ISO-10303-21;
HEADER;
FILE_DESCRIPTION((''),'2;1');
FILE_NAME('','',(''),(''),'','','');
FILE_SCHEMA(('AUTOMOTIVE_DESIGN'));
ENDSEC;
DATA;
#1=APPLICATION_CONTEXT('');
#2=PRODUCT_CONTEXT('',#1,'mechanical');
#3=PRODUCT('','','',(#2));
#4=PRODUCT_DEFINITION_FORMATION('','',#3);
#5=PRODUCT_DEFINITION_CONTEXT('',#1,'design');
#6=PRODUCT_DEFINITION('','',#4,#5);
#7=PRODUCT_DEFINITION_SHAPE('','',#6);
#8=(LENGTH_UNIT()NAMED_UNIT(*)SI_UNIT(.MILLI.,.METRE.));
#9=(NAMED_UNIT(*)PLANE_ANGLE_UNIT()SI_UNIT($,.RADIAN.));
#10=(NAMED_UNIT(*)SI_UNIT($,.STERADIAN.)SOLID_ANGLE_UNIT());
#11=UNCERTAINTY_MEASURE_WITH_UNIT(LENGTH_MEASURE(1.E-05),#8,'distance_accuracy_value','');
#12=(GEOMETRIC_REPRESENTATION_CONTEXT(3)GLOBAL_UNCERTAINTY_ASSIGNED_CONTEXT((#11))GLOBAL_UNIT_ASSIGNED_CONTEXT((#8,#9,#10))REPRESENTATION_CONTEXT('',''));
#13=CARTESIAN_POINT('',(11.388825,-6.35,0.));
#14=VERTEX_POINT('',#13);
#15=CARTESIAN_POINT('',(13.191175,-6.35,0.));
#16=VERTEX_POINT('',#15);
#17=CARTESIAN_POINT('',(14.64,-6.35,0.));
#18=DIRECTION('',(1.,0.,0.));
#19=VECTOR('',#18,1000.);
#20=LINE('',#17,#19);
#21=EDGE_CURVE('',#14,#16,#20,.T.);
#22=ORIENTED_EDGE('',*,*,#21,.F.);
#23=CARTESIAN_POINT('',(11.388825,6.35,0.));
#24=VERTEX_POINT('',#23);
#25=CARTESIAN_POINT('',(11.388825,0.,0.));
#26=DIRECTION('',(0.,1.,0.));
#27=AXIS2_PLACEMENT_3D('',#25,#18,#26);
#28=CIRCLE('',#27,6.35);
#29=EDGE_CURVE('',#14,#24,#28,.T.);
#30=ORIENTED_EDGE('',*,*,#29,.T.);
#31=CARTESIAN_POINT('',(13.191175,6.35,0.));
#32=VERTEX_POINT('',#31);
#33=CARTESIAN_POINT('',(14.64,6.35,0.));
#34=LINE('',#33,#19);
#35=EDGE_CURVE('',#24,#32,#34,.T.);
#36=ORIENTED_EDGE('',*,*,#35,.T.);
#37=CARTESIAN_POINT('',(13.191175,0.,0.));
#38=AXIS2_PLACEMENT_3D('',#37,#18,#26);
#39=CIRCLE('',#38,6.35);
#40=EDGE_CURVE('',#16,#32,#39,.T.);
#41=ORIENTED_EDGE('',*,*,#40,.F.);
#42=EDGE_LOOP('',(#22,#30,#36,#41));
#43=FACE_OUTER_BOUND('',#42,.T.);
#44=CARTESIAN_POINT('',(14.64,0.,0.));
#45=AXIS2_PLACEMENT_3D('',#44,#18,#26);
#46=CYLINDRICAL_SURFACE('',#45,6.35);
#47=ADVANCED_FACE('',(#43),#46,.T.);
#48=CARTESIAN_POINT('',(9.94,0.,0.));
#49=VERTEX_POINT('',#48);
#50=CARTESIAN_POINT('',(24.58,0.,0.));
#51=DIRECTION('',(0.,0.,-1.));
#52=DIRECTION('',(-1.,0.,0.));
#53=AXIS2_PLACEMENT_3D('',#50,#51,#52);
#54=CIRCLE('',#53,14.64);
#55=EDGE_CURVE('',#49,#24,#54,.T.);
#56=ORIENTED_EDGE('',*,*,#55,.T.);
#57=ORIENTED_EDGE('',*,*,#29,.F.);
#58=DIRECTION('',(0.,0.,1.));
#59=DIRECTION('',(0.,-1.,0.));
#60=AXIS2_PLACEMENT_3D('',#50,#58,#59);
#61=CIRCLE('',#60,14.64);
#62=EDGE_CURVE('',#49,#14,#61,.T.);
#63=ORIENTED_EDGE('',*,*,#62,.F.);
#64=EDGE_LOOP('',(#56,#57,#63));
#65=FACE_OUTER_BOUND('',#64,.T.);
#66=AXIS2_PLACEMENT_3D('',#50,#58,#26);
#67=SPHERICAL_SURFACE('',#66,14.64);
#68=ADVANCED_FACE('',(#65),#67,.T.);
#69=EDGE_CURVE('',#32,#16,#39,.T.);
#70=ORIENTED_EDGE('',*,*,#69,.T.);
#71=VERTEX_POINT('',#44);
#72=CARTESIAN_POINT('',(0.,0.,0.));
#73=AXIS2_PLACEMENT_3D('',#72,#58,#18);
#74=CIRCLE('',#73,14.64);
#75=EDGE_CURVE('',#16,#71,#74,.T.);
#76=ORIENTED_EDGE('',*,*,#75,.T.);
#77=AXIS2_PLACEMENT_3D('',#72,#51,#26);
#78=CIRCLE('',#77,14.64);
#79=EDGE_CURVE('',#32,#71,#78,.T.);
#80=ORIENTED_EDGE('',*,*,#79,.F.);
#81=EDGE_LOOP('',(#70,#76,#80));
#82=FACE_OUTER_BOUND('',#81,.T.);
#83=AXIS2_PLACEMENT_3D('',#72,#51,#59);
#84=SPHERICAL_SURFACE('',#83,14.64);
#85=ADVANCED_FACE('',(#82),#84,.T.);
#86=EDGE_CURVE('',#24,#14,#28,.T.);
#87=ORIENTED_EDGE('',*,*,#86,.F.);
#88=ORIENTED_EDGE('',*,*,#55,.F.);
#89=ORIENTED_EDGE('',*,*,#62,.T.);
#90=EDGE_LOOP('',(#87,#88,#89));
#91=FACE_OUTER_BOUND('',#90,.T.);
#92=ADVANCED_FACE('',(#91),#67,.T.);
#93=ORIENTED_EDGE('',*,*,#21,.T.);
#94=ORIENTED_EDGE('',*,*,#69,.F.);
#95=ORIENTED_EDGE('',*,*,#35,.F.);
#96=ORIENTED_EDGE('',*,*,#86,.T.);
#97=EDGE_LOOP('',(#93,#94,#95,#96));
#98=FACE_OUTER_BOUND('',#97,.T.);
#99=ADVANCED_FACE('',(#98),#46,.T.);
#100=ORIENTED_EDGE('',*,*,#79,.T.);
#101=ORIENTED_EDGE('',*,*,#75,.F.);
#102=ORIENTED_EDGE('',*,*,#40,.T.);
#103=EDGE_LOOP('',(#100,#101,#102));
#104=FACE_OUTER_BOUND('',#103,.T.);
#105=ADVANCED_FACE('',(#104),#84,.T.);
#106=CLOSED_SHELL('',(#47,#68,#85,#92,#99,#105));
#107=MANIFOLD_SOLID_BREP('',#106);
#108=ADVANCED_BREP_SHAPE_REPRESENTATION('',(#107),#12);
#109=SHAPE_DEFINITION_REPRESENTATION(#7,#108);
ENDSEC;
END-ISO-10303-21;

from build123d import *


with BuildPart() as part:
    # Sketch1 → Revolve4 (revolve)
    with BuildSketch(Plane.XY):
        with BuildLine():
            Line((14.64, 0), (9.94, 0))
            ThreePointArc((9.94, 0), (10.306801284, 3.256593068), (11.38882492, 6.35))
            Line((11.38882492, 6.35), (13.19117508, 6.35))
            ThreePointArc((13.19117508, 6.35), (14.273198716, 3.256593068), (14.64, 0))
        make_face()
    revolve(axis=Axis((14.64, 0, 0), (-1, 0, 0)))


solid = part.part
